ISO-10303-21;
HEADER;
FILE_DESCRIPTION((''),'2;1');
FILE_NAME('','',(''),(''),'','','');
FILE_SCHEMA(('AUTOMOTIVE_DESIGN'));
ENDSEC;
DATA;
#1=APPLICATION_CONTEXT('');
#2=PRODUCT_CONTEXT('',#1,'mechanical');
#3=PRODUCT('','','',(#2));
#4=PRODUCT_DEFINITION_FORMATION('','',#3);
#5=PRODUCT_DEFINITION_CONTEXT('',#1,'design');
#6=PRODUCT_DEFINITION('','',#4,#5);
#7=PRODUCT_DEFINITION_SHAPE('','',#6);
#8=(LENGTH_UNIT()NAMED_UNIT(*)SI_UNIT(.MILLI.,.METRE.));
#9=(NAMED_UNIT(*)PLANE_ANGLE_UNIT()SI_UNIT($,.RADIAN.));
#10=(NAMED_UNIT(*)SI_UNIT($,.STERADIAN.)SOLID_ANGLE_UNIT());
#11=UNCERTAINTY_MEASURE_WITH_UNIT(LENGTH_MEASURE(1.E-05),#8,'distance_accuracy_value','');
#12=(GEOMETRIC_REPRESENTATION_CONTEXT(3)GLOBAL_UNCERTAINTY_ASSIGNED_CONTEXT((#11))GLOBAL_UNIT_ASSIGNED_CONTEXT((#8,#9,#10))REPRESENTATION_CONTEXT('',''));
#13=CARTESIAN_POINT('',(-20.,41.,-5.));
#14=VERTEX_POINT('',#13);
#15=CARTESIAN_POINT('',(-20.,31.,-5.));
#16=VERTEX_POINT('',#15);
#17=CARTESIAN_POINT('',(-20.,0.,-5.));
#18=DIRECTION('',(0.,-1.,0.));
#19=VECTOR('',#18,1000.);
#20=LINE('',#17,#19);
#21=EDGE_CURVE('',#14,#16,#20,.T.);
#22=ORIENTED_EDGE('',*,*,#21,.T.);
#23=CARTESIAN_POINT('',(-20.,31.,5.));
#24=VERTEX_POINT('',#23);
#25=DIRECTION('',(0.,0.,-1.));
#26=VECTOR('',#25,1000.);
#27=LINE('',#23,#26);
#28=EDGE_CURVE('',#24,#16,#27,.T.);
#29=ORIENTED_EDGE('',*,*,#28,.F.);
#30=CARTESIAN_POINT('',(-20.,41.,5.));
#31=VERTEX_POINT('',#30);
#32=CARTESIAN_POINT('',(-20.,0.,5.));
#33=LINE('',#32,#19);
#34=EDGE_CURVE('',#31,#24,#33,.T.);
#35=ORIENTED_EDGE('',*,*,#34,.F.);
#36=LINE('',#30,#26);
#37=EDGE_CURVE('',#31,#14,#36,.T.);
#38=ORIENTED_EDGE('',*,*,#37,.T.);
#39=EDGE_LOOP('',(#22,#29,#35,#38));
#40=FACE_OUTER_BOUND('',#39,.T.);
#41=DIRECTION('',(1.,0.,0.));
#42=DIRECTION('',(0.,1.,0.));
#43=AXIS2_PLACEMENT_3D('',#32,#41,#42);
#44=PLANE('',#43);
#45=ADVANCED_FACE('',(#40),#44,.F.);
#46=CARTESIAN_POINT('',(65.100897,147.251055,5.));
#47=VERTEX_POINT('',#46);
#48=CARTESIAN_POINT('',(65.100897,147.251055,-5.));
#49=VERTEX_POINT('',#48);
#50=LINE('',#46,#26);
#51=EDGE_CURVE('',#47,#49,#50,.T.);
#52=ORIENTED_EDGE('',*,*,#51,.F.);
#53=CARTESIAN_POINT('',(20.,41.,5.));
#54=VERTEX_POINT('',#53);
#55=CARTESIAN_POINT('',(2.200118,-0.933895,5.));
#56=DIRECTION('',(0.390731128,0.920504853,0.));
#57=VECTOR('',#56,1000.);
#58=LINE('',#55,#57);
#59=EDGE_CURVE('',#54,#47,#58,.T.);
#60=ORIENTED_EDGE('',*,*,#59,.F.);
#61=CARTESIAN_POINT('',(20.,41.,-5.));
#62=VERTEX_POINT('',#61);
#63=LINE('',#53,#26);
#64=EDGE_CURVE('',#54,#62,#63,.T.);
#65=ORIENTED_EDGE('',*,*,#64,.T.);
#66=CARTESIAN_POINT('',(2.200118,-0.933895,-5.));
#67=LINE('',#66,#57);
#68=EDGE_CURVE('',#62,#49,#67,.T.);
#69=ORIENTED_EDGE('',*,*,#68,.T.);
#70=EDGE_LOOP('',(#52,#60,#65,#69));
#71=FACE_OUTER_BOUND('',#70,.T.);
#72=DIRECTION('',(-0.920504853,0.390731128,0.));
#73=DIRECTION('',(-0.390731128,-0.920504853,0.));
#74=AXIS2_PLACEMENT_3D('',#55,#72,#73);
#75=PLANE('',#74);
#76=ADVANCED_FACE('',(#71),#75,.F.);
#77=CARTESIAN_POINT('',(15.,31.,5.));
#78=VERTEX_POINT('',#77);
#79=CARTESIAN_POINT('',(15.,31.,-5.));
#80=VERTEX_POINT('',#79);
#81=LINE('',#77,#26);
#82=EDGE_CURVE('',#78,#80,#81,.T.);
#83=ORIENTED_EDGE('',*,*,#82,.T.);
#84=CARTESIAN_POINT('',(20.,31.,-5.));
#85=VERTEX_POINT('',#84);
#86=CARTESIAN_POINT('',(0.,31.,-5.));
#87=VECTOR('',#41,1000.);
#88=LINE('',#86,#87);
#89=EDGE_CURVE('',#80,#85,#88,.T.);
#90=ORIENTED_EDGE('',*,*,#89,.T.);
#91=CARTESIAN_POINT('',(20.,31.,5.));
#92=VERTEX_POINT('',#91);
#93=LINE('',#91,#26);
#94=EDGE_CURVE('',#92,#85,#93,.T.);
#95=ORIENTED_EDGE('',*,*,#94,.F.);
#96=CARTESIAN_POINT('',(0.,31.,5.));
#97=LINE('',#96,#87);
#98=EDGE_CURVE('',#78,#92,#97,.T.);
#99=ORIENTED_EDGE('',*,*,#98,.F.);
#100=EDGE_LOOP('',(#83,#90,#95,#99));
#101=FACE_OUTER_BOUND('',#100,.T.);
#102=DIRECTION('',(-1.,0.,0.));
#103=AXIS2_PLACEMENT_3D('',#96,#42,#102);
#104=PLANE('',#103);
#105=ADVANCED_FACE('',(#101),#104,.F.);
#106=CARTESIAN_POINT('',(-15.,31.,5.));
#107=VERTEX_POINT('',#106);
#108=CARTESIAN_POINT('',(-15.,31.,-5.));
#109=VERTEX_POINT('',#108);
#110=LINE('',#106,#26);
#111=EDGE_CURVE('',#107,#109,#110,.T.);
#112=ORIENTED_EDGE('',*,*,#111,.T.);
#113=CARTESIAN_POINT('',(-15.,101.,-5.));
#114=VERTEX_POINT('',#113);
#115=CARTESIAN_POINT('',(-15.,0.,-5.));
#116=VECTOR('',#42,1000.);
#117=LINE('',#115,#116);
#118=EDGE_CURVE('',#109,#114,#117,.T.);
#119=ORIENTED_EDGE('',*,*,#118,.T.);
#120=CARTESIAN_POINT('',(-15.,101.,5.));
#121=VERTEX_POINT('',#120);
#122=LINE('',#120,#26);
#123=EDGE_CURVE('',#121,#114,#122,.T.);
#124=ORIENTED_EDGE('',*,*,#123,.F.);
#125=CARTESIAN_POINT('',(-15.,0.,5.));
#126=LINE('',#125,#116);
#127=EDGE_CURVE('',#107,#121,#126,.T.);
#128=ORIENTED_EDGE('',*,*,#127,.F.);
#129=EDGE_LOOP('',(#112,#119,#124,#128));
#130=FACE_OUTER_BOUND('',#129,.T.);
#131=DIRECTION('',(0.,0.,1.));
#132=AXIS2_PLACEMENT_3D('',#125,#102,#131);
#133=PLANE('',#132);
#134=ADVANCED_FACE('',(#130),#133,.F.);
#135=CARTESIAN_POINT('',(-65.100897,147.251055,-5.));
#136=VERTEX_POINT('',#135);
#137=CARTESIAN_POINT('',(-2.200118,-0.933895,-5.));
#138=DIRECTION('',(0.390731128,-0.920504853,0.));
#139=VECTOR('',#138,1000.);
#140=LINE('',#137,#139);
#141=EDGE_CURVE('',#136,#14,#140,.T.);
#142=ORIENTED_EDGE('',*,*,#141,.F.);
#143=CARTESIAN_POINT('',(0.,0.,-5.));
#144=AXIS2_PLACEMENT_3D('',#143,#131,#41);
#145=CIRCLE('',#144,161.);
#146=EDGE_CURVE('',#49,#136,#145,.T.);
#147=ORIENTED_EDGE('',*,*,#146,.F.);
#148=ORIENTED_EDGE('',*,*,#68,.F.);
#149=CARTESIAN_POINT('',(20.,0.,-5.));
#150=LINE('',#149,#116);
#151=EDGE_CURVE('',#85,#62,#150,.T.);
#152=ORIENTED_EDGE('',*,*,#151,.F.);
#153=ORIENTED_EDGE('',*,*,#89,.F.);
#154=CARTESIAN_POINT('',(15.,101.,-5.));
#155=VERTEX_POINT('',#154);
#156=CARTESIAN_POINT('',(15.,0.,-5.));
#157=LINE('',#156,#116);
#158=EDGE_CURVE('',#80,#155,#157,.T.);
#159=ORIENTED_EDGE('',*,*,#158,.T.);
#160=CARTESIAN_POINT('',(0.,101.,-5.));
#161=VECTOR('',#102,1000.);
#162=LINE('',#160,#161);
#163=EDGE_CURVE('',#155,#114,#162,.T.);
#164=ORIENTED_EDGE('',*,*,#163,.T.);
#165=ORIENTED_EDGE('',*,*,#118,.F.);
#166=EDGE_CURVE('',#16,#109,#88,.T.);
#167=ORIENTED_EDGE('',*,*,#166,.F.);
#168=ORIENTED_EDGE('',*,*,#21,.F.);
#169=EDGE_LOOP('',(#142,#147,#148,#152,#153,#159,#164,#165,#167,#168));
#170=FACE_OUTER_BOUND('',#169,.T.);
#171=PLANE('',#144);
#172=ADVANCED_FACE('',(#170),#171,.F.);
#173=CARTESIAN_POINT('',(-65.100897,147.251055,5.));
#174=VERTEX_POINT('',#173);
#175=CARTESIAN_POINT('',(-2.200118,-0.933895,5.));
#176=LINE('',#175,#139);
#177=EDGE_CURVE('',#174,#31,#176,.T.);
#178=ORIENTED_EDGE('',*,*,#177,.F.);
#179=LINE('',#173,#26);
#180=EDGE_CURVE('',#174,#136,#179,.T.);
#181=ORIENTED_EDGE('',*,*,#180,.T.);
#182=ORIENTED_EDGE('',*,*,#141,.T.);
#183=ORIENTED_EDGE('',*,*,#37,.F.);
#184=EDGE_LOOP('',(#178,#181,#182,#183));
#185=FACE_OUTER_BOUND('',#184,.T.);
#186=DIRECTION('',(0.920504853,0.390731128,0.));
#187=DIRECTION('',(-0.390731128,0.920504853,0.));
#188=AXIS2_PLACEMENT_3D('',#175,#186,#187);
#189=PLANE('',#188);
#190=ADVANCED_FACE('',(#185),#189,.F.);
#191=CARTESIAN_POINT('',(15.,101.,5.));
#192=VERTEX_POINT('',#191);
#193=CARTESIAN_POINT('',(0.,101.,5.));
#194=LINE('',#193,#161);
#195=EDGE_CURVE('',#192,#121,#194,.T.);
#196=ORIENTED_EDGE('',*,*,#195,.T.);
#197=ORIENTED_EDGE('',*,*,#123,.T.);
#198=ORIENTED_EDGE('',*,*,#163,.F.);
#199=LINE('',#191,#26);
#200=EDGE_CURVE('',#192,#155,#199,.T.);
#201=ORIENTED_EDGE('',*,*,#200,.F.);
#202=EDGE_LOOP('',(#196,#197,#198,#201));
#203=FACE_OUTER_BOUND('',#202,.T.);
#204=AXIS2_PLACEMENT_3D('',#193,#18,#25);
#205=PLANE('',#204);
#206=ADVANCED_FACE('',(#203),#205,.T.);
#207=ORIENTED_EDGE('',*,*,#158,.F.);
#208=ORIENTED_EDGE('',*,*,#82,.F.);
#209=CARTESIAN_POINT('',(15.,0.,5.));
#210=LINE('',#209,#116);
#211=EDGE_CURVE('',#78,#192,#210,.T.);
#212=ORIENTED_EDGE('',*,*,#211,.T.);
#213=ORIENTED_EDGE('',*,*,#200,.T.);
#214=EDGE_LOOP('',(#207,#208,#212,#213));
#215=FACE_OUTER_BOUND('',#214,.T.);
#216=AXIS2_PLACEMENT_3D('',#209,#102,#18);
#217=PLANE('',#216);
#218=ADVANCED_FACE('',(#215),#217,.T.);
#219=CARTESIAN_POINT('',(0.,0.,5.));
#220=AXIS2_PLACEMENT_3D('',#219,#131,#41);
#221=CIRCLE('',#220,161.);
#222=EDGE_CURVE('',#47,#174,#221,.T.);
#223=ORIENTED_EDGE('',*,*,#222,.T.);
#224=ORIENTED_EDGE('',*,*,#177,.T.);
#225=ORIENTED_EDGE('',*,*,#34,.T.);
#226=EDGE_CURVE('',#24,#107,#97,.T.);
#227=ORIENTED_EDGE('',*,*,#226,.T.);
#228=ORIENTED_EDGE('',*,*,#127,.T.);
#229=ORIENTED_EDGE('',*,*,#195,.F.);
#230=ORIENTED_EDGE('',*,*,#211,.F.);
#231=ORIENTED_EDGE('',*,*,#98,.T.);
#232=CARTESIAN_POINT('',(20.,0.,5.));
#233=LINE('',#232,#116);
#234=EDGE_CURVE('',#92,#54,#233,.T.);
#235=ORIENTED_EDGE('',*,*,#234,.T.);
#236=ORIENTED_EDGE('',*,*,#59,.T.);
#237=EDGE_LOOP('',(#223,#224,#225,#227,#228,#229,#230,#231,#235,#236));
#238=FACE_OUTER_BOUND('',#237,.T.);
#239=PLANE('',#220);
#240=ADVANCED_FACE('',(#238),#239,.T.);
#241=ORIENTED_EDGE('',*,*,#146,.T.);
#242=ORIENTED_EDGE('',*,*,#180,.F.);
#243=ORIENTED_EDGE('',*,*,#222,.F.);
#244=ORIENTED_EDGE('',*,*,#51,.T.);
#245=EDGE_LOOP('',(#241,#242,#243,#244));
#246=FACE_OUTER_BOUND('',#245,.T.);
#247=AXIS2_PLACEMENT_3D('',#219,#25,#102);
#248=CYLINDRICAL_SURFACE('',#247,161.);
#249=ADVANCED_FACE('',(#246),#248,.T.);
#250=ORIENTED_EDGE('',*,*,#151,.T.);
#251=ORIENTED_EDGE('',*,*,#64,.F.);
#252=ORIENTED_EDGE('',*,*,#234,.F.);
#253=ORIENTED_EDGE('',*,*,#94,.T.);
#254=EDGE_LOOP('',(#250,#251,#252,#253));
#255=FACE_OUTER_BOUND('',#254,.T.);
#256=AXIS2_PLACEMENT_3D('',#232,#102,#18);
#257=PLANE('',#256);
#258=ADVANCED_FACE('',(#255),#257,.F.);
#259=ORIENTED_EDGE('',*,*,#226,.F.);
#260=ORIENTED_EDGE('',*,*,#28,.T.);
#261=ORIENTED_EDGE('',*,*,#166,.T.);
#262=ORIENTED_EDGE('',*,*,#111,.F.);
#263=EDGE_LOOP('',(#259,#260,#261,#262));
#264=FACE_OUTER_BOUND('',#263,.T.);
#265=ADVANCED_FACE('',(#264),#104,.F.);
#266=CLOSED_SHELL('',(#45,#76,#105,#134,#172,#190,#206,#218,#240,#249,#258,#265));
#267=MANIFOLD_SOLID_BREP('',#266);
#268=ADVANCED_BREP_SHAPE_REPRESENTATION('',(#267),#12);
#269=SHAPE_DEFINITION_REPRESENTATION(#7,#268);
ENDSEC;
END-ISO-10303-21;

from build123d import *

# Parameters (mm, degrees)
BOSS_EXTRUDE2_DEPTH = 5


with BuildPart() as part:
    # Sketch1 → Boss-Extrude2 (new, symmetric)
    with BuildSketch(Plane.XY):
        with BuildLine():
            ThreePointArc((65.10089705, 147.251055016), (0, 161), (-65.10089705, 147.251055016))
            Line((-65.10089705, 147.251055016), (-20, 41))
            Line((-20, 41), (-20, 31))
            Line((-20, 31), (-15, 31))
            Line((-15, 31), (-15, 101))
            Line((-15, 101), (15, 101))
            Line((15, 101), (15, 31))
            Line((15, 31), (20, 31))
            Line((20, 31), (20, 41))
            Line((20, 41), (65.10089705, 147.251055016))
        make_face()
    extrude(amount=BOSS_EXTRUDE2_DEPTH, both=True)


solid = part.part
